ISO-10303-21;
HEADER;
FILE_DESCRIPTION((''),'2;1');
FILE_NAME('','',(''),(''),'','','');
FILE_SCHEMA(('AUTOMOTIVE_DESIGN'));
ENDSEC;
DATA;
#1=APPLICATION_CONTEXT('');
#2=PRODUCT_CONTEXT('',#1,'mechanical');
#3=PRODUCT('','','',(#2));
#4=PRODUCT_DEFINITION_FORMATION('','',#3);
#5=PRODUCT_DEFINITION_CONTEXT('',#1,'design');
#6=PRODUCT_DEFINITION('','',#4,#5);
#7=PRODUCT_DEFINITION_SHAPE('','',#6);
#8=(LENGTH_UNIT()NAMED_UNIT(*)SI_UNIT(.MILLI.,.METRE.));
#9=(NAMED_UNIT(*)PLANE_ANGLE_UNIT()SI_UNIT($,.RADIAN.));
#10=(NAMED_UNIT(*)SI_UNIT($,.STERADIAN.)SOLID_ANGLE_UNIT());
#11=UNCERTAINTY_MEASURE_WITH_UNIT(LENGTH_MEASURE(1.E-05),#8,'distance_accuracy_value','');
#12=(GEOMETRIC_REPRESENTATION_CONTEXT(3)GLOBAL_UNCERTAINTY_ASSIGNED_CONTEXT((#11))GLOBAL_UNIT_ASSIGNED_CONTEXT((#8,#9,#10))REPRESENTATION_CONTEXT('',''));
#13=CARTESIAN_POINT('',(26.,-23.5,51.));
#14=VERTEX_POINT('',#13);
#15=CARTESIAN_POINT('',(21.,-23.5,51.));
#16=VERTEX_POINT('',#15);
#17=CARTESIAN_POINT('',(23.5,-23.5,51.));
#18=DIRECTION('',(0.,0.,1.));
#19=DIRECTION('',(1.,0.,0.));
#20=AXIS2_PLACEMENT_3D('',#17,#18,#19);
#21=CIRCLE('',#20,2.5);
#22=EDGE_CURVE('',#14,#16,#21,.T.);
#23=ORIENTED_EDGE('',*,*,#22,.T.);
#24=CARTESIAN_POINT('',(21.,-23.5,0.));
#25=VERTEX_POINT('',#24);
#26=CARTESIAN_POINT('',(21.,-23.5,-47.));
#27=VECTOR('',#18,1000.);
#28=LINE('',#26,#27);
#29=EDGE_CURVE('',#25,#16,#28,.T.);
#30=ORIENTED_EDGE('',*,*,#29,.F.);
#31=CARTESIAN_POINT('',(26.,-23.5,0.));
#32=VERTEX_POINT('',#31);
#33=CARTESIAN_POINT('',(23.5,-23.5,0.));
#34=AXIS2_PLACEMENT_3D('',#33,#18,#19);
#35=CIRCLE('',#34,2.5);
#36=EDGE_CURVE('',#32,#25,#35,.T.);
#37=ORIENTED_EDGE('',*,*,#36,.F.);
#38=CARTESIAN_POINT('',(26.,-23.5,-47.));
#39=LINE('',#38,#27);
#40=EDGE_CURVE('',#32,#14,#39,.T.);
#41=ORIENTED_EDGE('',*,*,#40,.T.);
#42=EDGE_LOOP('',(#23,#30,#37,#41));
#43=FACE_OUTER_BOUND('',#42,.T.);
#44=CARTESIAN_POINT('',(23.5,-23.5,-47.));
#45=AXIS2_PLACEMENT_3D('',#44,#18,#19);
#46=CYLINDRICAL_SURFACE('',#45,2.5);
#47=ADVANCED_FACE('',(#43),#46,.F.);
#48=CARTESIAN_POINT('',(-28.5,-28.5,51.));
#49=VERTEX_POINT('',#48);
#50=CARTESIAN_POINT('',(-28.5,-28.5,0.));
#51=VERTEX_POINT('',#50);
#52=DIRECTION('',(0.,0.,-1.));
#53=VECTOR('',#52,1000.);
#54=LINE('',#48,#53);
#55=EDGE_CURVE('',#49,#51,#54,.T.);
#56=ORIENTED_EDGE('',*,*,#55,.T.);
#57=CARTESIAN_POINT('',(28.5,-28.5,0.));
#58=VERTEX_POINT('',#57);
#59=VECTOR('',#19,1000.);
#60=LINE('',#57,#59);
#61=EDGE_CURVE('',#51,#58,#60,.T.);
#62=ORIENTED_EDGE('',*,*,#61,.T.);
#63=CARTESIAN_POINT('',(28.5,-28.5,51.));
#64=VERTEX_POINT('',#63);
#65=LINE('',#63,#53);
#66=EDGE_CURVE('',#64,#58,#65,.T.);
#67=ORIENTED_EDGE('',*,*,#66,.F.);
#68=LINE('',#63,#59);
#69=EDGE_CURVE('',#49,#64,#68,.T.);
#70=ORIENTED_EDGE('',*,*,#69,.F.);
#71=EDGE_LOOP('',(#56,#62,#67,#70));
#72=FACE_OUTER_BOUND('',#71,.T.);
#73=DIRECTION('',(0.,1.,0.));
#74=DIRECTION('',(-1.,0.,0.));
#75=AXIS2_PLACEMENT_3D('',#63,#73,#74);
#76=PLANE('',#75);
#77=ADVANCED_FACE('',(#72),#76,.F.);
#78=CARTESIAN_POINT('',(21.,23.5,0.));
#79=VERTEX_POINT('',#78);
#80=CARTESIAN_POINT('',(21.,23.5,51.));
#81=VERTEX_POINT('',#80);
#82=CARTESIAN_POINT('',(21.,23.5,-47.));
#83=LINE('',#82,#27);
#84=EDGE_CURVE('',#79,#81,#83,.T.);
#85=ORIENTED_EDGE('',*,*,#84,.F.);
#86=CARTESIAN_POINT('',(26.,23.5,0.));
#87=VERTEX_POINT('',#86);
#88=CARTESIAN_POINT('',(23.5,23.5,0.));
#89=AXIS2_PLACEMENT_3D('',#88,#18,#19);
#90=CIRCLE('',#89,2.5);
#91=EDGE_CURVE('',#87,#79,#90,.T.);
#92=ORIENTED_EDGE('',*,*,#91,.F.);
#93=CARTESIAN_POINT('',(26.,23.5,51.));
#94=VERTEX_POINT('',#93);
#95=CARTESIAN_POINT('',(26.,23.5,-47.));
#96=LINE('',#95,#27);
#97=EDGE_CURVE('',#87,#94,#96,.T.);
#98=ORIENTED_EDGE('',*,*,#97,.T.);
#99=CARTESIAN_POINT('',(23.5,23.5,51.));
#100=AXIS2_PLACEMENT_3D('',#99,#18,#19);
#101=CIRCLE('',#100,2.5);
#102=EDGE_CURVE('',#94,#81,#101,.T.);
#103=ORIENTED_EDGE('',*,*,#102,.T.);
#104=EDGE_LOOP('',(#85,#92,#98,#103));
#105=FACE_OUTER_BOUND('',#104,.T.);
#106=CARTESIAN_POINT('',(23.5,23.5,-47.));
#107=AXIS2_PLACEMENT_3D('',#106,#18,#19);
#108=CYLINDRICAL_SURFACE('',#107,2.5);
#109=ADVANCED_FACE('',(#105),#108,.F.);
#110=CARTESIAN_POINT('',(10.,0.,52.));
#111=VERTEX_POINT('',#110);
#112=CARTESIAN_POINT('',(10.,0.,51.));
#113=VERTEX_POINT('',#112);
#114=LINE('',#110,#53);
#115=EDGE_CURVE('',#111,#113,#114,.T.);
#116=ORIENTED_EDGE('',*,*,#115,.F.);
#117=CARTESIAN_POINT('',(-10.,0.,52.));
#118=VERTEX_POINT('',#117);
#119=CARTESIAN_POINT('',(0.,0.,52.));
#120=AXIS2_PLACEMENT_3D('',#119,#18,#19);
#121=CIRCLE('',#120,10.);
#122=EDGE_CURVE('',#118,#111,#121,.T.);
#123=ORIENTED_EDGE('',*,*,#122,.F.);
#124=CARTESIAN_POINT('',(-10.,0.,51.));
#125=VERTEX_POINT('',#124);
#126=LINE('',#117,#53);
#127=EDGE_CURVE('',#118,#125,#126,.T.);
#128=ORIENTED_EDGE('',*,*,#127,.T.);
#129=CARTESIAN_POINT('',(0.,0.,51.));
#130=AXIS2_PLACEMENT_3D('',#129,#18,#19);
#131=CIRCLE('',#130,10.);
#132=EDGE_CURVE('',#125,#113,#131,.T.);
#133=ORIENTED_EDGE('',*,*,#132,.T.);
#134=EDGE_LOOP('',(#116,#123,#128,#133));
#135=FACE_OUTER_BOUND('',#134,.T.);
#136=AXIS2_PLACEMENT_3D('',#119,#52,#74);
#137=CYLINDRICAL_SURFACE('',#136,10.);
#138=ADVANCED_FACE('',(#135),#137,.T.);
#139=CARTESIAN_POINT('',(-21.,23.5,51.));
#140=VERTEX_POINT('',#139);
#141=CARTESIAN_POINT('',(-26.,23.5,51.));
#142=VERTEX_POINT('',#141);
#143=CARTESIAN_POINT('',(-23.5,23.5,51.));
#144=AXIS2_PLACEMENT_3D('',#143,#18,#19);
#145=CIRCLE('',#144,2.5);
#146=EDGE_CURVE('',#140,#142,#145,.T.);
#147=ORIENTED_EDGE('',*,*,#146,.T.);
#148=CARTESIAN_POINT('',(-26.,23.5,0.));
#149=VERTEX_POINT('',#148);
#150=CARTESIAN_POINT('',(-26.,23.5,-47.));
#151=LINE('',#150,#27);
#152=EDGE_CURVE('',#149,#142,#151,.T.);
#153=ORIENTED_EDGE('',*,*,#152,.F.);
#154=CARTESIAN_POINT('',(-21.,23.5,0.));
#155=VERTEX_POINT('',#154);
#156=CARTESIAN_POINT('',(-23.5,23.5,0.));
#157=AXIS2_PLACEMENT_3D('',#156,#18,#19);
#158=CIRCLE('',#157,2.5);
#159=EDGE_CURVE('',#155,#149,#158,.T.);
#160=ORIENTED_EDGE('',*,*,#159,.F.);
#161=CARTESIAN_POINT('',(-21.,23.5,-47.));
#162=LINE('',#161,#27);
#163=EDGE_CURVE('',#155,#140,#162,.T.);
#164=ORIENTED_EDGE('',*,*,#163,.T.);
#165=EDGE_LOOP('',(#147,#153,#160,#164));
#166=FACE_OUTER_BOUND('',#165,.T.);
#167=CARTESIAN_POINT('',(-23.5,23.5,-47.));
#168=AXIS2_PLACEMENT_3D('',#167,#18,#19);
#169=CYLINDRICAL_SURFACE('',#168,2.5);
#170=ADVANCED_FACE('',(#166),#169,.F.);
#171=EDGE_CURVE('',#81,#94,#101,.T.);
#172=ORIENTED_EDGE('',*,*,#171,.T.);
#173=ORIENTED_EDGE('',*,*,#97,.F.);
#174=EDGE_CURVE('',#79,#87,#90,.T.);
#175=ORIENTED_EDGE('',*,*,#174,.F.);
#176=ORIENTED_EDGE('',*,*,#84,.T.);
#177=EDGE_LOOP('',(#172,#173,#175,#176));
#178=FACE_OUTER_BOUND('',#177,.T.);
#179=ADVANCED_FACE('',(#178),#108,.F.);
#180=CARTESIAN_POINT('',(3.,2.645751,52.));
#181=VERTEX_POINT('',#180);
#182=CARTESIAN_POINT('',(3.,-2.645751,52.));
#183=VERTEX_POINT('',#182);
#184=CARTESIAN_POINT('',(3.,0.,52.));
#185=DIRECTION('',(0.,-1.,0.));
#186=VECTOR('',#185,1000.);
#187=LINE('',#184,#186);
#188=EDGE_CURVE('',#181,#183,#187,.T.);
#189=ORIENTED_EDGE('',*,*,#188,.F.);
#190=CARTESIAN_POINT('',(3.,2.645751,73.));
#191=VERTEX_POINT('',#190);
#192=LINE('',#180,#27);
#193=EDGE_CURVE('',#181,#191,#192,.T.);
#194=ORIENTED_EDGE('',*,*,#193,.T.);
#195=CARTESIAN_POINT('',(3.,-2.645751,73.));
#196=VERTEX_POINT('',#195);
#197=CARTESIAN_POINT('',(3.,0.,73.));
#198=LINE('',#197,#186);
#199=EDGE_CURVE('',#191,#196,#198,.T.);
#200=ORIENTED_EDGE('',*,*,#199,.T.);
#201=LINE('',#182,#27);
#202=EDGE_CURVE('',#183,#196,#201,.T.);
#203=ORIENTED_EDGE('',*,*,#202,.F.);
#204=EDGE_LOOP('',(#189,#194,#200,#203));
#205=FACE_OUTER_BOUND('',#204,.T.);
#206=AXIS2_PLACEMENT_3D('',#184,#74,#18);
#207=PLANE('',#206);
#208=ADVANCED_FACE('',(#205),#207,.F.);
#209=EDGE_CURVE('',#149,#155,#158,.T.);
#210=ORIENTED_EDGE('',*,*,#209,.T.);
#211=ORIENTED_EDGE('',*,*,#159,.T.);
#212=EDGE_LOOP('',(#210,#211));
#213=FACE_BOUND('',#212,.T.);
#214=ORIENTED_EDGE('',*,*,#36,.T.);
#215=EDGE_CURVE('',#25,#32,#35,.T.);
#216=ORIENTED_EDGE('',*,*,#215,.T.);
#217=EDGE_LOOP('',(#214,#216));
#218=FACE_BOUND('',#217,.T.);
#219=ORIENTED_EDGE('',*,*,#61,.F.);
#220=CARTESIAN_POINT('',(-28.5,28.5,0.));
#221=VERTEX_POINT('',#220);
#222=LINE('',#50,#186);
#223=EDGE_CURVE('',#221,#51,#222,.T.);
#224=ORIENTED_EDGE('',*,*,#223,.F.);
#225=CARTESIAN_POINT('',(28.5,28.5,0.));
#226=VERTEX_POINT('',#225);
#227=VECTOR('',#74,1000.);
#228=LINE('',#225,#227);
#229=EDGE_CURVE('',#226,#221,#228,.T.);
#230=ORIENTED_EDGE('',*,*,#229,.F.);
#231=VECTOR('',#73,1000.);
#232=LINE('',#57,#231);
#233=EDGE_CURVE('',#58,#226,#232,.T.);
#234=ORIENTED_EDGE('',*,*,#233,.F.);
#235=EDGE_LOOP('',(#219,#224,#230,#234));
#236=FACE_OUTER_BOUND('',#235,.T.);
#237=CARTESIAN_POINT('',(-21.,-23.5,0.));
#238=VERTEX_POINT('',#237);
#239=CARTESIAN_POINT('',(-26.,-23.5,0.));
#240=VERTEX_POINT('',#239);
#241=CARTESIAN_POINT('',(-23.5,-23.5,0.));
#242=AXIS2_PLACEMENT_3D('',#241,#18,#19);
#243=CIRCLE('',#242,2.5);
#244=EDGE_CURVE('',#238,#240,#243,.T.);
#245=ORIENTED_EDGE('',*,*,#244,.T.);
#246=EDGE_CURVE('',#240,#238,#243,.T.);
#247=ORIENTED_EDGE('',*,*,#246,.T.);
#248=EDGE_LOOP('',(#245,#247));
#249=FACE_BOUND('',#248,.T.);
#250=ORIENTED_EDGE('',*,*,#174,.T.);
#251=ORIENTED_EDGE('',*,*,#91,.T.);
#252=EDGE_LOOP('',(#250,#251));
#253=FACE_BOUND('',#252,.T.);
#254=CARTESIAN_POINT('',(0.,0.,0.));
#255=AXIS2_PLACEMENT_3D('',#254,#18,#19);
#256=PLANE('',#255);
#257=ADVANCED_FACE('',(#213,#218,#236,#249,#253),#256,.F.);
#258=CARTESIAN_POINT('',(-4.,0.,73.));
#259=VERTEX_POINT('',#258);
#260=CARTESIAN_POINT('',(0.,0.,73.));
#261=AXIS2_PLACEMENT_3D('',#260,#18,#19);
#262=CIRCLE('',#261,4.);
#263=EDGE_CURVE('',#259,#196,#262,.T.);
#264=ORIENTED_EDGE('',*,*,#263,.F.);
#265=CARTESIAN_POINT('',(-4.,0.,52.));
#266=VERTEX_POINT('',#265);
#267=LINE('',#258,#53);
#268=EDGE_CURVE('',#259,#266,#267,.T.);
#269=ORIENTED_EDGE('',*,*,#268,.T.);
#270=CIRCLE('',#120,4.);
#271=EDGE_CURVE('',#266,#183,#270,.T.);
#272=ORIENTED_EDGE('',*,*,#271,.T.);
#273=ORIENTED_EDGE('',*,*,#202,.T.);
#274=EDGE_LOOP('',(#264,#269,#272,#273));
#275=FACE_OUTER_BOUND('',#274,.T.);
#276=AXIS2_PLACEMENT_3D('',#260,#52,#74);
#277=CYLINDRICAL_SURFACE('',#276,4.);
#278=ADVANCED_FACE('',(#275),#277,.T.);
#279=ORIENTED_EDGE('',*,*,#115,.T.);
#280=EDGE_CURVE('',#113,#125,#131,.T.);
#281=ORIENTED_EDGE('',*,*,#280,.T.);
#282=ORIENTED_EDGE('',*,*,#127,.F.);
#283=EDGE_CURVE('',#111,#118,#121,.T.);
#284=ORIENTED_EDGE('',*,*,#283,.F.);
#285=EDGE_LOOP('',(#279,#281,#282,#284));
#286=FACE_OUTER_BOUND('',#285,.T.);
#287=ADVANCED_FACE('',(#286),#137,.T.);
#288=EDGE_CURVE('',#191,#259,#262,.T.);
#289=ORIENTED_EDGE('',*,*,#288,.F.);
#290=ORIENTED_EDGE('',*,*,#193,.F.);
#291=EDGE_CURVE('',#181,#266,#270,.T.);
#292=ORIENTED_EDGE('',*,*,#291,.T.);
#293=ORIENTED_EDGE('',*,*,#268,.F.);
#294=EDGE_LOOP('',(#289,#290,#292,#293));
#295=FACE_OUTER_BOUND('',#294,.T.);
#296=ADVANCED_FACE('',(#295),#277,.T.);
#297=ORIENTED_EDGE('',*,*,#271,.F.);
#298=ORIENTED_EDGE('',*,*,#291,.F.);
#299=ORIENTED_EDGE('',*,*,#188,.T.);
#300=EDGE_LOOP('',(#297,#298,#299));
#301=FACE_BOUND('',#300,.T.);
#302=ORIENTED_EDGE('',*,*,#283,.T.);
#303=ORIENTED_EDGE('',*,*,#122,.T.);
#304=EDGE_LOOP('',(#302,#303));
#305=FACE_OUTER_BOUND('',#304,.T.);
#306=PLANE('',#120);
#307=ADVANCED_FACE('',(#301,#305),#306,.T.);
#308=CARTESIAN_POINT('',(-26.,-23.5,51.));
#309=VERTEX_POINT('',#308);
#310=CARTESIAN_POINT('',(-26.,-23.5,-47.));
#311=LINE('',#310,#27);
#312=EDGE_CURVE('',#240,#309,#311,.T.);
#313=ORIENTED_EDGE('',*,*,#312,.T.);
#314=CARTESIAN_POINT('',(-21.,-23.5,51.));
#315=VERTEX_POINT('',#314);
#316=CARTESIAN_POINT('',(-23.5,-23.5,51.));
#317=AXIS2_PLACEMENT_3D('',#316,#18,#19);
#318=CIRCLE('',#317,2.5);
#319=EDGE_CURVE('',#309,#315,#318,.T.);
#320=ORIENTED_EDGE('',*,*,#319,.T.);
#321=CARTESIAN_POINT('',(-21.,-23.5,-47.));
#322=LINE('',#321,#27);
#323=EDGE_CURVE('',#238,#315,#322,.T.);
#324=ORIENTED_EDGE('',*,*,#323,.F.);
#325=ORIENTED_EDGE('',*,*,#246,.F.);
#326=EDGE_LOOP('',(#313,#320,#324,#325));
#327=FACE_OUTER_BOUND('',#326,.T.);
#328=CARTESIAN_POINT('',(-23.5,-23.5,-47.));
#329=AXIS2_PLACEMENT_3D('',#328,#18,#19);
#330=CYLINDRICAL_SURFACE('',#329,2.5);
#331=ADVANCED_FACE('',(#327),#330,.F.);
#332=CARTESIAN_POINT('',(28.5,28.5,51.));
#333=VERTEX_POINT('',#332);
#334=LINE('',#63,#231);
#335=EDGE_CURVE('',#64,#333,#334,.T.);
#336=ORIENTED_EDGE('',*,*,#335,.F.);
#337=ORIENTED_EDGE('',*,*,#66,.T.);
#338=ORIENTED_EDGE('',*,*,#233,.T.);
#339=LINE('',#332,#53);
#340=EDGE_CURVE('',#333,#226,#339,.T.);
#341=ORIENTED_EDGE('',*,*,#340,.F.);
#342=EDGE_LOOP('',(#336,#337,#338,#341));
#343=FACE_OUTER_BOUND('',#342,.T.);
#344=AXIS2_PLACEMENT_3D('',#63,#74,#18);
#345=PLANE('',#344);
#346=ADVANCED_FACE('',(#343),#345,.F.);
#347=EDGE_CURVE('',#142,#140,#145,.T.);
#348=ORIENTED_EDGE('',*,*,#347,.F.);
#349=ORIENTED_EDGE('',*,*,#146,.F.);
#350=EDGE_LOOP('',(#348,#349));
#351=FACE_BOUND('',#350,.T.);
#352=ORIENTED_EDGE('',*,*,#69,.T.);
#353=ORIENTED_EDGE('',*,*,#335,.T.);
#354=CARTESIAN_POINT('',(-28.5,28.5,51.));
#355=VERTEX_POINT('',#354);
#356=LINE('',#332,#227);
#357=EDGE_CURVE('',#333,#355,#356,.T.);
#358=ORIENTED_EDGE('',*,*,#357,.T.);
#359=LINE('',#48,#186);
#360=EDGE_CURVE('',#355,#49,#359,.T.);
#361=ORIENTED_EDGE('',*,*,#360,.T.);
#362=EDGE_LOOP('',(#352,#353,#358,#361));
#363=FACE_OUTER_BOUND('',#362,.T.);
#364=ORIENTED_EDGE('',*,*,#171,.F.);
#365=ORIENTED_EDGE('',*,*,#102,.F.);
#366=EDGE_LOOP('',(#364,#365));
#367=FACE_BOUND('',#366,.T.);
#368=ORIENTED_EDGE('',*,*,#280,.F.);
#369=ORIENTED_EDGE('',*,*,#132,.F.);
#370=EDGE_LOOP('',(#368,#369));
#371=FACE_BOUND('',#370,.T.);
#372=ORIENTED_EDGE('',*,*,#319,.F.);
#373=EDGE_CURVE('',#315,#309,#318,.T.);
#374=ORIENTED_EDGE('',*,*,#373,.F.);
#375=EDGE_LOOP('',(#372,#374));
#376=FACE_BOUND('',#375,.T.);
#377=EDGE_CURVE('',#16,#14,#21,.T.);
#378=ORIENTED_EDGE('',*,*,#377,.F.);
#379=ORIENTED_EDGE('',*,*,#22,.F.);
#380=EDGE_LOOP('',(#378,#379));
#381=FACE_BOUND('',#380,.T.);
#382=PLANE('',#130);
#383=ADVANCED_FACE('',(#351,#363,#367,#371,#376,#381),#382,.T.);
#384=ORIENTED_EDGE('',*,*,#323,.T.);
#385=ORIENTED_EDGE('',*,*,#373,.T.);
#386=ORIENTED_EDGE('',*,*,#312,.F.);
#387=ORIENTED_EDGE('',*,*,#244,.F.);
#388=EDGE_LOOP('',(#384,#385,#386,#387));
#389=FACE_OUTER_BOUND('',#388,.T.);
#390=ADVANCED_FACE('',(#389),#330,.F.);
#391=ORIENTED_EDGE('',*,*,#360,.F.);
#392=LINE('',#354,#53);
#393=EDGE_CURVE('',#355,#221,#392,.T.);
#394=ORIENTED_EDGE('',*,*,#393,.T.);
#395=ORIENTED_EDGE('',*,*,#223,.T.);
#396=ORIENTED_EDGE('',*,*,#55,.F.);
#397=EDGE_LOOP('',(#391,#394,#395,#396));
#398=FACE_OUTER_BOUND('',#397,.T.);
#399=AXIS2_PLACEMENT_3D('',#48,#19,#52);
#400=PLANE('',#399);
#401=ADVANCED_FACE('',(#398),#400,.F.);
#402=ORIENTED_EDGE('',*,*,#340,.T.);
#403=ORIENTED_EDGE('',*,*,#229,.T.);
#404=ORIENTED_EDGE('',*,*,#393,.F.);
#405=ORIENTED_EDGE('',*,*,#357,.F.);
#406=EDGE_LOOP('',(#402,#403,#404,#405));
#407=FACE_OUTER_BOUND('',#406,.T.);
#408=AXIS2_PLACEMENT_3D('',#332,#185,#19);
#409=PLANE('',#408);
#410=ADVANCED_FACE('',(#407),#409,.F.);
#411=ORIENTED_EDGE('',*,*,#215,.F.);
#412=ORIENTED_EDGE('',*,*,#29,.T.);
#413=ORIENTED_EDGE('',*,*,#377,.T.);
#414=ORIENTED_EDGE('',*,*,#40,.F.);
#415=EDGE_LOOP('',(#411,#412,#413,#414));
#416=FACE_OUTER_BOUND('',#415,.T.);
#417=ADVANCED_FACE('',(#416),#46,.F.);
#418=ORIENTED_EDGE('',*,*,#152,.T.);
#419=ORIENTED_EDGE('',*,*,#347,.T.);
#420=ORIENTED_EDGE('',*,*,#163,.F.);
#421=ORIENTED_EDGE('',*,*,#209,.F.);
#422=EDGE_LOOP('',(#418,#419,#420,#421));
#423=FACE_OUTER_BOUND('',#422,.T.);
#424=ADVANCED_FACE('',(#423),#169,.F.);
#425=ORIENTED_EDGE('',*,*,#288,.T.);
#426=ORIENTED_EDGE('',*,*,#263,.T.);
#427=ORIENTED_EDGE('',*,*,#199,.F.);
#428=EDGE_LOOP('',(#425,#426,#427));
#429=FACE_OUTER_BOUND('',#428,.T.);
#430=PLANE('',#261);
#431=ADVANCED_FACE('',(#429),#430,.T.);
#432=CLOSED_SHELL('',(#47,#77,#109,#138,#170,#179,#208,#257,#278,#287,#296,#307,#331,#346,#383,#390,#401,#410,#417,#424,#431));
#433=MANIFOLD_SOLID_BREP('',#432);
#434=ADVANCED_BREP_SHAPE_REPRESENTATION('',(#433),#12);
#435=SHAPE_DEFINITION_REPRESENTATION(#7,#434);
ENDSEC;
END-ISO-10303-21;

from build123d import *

# Parameters (mm, degrees)
SKETCH1_W           = 57
SKETCH1_H           = 57
BOSS_EXTRUDE1_DEPTH = 51
SKETCH2_R           = 2.5
CUT_EXTRUDE1_DEPTH  = 98
SKETCH4_R           = 10
BOSS_EXTRUDE2_DEPTH = 1
SKETCH5_R           = 4
BOSS_EXTRUDE3_DEPTH = 21
CUT_EXTRUDE2_DEPTH  = 21


with BuildPart() as part:
    # Sketch1 → Boss-Extrude1 (new body)
    with BuildSketch(Plane.XY):
        Rectangle(SKETCH1_W, SKETCH1_H)
    extrude(amount=BOSS_EXTRUDE1_DEPTH)

    # Sketch2 → Cut-Extrude1 (cut)
    with BuildSketch(Plane.XY.offset(51)):
        with Locations((-23.5, 23.5)):
            Circle(SKETCH2_R)
        with Locations((23.5, 23.5)):
            Circle(SKETCH2_R)
        with Locations((23.5, -23.5)):
            Circle(SKETCH2_R)
        with Locations((-23.5, -23.5)):
            Circle(SKETCH2_R)
    extrude(amount=-CUT_EXTRUDE1_DEPTH, mode=Mode.SUBTRACT)

    # Sketch4 → Boss-Extrude2 (add)
    with BuildSketch(Plane.XY.offset(51)):
        Circle(SKETCH4_R)
    extrude(amount=BOSS_EXTRUDE2_DEPTH)

    # Sketch5 → Boss-Extrude3 (add)
    with BuildSketch(Plane.XY.offset(52)):
        with Locations(Location((0, 0, 0), (0, 0, 180))):
            Circle(SKETCH5_R)
    extrude(amount=BOSS_EXTRUDE3_DEPTH)

    # Sketch6 → Cut-Extrude2 (cut)
    with BuildSketch(Plane.XY.offset(73)):
        Polygon((3, 101.241638907), (3, 2.645751311), (3, -2.645751311), (3, -101.241638907), (200.191775192, -101.241638907), (200.191775192, 101.241638907), align=None)
    extrude(amount=-CUT_EXTRUDE2_DEPTH, mode=Mode.SUBTRACT)


solid = part.part
